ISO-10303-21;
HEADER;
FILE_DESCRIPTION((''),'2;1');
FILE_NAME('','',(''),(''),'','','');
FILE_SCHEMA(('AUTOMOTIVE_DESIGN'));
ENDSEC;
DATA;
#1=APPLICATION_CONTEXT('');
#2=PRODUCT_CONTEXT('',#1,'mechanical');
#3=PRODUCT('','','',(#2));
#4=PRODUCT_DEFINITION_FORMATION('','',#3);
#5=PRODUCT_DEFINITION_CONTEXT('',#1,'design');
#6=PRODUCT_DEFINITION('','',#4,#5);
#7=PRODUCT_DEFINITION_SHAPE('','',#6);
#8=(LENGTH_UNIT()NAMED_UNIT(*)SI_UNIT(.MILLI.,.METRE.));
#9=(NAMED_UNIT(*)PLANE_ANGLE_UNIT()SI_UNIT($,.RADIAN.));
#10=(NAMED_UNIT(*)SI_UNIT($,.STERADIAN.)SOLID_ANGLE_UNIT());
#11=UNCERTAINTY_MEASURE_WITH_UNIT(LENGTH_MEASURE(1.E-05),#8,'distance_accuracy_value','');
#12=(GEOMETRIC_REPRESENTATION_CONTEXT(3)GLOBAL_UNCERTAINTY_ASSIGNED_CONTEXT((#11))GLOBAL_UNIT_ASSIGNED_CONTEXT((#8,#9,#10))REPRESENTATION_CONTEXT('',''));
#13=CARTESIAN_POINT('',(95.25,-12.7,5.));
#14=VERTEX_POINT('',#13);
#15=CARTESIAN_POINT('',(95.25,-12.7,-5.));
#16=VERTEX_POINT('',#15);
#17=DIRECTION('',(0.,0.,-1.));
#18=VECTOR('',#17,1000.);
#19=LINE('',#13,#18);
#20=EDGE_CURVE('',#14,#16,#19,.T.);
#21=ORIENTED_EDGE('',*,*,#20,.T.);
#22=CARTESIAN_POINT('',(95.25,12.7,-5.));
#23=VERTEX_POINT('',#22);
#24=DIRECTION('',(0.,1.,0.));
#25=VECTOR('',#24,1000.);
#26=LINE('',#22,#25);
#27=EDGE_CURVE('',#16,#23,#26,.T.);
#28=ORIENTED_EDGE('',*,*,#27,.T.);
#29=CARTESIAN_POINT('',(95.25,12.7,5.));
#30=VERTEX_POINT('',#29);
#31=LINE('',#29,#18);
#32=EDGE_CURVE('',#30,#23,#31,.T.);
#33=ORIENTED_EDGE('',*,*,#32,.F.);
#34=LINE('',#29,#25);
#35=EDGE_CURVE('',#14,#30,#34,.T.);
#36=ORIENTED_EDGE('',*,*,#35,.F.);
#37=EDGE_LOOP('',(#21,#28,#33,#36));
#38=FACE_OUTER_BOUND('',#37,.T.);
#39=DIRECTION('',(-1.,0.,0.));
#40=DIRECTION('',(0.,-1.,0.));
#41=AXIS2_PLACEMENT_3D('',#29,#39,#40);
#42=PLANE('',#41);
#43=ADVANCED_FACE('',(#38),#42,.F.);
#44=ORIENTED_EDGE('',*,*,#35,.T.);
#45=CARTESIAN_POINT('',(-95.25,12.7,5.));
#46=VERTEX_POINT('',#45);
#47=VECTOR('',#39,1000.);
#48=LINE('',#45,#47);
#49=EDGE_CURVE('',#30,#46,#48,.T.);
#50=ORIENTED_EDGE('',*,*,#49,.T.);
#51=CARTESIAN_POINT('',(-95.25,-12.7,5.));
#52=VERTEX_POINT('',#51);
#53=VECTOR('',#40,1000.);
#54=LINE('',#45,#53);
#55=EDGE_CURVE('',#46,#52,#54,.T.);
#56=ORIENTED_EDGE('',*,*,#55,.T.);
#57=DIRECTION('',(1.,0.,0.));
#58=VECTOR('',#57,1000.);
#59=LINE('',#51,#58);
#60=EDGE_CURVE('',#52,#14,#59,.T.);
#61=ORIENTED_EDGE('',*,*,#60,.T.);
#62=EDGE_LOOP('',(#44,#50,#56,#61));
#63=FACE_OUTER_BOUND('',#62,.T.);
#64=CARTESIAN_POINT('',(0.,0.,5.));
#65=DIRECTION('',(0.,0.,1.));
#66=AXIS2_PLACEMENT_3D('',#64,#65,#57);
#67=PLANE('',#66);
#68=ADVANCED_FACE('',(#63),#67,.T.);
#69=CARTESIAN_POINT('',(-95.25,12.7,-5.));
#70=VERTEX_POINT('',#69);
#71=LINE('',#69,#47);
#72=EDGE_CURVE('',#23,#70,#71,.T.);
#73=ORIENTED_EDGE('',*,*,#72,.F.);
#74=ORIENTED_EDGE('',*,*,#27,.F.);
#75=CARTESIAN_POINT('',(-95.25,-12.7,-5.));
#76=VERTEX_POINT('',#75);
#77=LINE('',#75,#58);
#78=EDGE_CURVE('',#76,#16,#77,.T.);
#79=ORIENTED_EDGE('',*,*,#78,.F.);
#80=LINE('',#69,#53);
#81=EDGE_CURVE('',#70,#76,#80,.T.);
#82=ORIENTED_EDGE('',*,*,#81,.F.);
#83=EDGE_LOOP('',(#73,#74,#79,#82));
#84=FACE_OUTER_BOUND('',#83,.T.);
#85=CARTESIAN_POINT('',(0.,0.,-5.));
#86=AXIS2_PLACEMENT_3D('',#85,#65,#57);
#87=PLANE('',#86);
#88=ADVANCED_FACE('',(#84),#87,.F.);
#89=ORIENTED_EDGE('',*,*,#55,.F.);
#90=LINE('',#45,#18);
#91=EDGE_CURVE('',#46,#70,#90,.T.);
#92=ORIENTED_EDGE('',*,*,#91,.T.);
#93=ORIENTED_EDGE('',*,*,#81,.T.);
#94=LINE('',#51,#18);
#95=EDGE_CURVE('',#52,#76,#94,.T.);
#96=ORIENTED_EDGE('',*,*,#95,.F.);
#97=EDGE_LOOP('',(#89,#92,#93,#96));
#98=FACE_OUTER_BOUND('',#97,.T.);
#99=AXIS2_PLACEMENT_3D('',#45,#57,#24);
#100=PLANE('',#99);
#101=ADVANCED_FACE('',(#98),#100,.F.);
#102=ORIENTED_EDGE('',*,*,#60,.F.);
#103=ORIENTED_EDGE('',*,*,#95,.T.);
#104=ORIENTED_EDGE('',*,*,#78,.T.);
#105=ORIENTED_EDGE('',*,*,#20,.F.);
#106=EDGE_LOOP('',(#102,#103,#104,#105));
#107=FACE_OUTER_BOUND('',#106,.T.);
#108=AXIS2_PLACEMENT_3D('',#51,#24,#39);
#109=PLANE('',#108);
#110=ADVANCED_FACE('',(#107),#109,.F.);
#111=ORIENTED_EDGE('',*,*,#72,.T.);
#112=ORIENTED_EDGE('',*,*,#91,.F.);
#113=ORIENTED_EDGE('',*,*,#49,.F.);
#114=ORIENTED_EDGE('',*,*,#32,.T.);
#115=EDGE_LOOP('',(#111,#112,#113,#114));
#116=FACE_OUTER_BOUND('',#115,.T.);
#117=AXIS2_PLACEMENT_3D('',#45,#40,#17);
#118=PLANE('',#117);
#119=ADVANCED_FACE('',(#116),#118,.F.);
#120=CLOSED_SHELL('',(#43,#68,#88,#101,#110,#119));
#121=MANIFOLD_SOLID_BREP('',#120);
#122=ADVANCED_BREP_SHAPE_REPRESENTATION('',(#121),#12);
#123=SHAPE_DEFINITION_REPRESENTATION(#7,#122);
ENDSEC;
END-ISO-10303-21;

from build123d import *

# Parameters (mm, degrees)
SKETCH1_W           = 190.5
SKETCH1_H           = 25.4
BOSS_EXTRUDE1_DEPTH = 5


with BuildPart() as part:
    # Sketch1 → Boss-Extrude1 (new, symmetric)
    with BuildSketch(Plane.XY):
        Rectangle(SKETCH1_W, SKETCH1_H)
    extrude(amount=BOSS_EXTRUDE1_DEPTH, both=True)


solid = part.part
